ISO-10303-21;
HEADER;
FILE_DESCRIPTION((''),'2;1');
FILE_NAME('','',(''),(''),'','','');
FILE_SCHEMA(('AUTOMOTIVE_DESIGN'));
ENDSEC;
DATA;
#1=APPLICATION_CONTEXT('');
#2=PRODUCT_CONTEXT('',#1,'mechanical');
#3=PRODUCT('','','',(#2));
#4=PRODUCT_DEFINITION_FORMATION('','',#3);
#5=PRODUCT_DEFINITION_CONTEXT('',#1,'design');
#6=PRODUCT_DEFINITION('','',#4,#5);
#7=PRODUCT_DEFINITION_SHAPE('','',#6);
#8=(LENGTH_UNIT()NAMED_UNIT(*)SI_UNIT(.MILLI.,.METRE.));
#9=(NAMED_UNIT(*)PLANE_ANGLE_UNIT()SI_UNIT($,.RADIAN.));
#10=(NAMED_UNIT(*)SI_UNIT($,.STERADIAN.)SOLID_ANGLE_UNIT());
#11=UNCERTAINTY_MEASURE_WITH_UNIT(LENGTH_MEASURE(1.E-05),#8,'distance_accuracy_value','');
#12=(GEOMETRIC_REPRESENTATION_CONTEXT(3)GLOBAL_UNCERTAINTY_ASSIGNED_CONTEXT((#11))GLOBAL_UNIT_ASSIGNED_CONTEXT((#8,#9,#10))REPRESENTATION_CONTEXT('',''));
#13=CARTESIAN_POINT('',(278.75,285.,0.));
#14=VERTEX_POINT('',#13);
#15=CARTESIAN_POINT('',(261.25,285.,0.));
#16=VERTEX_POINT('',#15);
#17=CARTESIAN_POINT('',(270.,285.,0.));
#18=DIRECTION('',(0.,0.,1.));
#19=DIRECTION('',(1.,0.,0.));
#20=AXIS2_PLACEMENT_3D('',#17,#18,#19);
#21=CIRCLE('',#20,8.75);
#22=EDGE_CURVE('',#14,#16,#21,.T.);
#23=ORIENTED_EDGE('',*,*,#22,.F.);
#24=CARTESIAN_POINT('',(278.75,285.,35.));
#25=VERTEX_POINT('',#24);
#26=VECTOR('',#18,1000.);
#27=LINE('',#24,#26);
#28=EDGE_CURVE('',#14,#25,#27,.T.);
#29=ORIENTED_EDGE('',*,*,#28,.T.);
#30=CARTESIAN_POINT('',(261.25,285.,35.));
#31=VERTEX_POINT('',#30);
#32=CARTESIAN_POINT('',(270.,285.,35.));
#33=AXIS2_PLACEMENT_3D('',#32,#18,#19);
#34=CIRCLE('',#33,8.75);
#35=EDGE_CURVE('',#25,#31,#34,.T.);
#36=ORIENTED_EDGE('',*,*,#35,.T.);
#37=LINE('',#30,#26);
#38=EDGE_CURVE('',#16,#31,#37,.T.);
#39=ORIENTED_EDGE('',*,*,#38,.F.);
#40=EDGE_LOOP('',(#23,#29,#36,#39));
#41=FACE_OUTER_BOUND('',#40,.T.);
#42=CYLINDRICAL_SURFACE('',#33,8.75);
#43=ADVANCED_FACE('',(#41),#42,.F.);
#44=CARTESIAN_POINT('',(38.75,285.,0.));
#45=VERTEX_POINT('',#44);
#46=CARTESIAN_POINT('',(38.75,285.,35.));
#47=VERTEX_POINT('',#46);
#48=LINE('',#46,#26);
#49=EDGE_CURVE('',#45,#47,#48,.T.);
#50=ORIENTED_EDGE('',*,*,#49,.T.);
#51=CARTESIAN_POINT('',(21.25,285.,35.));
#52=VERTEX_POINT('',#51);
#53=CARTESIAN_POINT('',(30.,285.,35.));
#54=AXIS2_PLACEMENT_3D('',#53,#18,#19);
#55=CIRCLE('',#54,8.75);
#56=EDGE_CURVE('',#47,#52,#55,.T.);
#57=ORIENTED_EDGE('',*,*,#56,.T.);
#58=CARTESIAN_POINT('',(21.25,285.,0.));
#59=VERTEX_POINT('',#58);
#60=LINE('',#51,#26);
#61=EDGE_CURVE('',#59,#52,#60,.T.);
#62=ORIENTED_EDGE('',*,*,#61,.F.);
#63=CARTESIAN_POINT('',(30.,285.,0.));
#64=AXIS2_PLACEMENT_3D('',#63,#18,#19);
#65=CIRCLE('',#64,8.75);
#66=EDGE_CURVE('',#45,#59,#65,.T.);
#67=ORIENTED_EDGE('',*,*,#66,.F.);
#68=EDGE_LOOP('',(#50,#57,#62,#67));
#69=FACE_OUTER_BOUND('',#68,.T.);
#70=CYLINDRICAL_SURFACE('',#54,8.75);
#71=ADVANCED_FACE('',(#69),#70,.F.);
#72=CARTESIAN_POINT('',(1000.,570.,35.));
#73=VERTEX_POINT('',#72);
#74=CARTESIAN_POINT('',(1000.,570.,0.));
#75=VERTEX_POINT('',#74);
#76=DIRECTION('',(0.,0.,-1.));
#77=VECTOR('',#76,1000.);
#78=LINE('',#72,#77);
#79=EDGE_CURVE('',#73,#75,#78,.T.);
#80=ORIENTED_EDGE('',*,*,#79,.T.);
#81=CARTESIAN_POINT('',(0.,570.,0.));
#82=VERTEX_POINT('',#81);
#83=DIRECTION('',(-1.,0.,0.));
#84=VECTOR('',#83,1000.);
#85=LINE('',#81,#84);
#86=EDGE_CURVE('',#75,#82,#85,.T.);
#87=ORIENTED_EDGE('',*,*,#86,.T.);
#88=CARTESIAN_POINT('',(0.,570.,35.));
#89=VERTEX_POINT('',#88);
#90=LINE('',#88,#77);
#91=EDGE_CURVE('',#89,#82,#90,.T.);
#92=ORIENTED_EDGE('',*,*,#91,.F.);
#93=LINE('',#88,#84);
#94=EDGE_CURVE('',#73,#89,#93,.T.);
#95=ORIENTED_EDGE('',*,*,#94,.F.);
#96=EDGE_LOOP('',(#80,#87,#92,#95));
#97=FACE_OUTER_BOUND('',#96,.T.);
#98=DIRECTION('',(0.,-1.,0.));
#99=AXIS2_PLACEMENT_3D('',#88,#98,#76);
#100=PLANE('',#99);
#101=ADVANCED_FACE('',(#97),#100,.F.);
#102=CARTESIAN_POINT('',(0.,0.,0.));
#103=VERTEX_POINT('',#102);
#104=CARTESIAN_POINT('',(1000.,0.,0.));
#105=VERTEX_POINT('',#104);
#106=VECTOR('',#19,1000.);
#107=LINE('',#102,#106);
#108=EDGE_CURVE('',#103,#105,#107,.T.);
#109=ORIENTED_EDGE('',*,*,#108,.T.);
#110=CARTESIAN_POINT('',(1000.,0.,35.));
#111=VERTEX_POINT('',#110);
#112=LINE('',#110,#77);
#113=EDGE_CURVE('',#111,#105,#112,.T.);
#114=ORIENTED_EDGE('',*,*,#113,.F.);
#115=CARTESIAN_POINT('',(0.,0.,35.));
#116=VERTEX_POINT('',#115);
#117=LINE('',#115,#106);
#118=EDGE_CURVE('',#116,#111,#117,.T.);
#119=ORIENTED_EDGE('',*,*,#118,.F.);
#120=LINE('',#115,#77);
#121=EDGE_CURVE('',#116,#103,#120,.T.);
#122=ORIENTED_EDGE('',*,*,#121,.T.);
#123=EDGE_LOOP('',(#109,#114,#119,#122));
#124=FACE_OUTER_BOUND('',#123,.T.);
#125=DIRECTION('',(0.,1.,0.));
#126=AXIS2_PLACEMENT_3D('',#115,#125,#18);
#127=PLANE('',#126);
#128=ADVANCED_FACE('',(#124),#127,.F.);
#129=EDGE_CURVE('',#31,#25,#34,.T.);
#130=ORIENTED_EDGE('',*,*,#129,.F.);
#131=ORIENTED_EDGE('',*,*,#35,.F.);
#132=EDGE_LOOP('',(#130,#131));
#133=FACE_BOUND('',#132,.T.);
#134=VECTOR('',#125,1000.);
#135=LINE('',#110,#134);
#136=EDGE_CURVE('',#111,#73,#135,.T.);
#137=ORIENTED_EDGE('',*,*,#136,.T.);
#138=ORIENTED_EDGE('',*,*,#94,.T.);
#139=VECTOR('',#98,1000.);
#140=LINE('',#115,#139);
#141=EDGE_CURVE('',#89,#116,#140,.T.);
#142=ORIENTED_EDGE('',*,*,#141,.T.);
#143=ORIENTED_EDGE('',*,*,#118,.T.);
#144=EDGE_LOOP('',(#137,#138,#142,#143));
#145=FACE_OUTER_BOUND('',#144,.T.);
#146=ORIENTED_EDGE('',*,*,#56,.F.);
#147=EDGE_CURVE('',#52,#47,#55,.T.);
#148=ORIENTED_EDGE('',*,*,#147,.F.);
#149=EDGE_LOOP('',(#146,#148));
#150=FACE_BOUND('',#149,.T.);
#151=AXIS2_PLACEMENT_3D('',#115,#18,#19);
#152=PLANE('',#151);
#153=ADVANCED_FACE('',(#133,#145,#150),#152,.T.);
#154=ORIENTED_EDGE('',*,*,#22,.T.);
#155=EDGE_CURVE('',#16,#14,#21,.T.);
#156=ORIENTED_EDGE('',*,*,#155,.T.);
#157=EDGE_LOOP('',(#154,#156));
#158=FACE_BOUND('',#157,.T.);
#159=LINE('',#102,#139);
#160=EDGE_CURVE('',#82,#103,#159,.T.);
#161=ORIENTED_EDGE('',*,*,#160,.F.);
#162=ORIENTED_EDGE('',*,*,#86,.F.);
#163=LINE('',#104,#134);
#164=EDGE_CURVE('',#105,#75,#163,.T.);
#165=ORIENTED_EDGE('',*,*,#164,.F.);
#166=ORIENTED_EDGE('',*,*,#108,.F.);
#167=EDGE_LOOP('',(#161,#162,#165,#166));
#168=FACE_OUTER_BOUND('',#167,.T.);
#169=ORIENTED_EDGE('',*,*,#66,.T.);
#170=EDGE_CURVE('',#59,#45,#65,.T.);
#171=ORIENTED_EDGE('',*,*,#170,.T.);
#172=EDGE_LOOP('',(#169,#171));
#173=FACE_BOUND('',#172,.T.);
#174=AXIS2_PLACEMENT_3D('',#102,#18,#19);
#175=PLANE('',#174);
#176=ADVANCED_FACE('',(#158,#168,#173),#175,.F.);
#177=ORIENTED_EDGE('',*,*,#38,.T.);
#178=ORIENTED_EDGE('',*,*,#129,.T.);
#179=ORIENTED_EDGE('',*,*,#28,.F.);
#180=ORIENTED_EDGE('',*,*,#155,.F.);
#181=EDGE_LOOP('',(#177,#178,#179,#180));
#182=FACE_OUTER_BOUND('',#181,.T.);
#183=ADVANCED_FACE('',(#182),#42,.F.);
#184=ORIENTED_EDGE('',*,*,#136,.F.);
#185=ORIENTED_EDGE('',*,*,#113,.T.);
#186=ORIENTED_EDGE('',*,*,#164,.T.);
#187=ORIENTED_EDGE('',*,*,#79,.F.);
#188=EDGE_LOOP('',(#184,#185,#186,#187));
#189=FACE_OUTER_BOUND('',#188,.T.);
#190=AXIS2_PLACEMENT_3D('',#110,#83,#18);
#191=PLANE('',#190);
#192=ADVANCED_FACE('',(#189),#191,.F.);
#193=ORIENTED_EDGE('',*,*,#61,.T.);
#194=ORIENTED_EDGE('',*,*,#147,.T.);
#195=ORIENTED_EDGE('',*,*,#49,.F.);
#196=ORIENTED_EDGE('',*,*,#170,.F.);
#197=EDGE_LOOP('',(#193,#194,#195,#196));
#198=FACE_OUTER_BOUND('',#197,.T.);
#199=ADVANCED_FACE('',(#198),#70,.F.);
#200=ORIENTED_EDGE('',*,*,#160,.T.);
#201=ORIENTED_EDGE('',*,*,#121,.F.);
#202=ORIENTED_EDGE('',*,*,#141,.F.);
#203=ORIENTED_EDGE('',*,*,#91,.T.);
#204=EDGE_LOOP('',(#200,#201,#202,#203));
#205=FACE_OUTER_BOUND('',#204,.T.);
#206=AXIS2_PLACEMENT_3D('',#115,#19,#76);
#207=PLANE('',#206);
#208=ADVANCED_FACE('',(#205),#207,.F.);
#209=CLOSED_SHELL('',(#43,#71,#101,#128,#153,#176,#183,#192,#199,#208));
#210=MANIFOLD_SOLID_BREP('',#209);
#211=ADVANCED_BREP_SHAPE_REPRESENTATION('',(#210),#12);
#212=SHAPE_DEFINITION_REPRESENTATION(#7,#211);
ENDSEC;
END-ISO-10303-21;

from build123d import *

# Parameters (mm, degrees)
SKETCH1_W           = 1000
SKETCH1_H           = 570
BOSS_EXTRUDE1_DEPTH = 35
M20_TAPPED_HOLE1_D  = 17.5


with BuildPart() as part:
    # Sketch1 → Boss-Extrude1 (new body)
    with BuildSketch(Plane.XY):
        with Locations((500, 285)):
            Rectangle(SKETCH1_W, SKETCH1_H)
    extrude(amount=BOSS_EXTRUDE1_DEPTH)

    # M20 Tapped Hole1 (through all)
    with Locations(Plane(origin=(30, 285, 35), x_dir=(1, 0, 0), z_dir=(0, 0, 1))):
        with Locations((0, 0), (240, 0)):
            Hole(M20_TAPPED_HOLE1_D / 2)


solid = part.part
